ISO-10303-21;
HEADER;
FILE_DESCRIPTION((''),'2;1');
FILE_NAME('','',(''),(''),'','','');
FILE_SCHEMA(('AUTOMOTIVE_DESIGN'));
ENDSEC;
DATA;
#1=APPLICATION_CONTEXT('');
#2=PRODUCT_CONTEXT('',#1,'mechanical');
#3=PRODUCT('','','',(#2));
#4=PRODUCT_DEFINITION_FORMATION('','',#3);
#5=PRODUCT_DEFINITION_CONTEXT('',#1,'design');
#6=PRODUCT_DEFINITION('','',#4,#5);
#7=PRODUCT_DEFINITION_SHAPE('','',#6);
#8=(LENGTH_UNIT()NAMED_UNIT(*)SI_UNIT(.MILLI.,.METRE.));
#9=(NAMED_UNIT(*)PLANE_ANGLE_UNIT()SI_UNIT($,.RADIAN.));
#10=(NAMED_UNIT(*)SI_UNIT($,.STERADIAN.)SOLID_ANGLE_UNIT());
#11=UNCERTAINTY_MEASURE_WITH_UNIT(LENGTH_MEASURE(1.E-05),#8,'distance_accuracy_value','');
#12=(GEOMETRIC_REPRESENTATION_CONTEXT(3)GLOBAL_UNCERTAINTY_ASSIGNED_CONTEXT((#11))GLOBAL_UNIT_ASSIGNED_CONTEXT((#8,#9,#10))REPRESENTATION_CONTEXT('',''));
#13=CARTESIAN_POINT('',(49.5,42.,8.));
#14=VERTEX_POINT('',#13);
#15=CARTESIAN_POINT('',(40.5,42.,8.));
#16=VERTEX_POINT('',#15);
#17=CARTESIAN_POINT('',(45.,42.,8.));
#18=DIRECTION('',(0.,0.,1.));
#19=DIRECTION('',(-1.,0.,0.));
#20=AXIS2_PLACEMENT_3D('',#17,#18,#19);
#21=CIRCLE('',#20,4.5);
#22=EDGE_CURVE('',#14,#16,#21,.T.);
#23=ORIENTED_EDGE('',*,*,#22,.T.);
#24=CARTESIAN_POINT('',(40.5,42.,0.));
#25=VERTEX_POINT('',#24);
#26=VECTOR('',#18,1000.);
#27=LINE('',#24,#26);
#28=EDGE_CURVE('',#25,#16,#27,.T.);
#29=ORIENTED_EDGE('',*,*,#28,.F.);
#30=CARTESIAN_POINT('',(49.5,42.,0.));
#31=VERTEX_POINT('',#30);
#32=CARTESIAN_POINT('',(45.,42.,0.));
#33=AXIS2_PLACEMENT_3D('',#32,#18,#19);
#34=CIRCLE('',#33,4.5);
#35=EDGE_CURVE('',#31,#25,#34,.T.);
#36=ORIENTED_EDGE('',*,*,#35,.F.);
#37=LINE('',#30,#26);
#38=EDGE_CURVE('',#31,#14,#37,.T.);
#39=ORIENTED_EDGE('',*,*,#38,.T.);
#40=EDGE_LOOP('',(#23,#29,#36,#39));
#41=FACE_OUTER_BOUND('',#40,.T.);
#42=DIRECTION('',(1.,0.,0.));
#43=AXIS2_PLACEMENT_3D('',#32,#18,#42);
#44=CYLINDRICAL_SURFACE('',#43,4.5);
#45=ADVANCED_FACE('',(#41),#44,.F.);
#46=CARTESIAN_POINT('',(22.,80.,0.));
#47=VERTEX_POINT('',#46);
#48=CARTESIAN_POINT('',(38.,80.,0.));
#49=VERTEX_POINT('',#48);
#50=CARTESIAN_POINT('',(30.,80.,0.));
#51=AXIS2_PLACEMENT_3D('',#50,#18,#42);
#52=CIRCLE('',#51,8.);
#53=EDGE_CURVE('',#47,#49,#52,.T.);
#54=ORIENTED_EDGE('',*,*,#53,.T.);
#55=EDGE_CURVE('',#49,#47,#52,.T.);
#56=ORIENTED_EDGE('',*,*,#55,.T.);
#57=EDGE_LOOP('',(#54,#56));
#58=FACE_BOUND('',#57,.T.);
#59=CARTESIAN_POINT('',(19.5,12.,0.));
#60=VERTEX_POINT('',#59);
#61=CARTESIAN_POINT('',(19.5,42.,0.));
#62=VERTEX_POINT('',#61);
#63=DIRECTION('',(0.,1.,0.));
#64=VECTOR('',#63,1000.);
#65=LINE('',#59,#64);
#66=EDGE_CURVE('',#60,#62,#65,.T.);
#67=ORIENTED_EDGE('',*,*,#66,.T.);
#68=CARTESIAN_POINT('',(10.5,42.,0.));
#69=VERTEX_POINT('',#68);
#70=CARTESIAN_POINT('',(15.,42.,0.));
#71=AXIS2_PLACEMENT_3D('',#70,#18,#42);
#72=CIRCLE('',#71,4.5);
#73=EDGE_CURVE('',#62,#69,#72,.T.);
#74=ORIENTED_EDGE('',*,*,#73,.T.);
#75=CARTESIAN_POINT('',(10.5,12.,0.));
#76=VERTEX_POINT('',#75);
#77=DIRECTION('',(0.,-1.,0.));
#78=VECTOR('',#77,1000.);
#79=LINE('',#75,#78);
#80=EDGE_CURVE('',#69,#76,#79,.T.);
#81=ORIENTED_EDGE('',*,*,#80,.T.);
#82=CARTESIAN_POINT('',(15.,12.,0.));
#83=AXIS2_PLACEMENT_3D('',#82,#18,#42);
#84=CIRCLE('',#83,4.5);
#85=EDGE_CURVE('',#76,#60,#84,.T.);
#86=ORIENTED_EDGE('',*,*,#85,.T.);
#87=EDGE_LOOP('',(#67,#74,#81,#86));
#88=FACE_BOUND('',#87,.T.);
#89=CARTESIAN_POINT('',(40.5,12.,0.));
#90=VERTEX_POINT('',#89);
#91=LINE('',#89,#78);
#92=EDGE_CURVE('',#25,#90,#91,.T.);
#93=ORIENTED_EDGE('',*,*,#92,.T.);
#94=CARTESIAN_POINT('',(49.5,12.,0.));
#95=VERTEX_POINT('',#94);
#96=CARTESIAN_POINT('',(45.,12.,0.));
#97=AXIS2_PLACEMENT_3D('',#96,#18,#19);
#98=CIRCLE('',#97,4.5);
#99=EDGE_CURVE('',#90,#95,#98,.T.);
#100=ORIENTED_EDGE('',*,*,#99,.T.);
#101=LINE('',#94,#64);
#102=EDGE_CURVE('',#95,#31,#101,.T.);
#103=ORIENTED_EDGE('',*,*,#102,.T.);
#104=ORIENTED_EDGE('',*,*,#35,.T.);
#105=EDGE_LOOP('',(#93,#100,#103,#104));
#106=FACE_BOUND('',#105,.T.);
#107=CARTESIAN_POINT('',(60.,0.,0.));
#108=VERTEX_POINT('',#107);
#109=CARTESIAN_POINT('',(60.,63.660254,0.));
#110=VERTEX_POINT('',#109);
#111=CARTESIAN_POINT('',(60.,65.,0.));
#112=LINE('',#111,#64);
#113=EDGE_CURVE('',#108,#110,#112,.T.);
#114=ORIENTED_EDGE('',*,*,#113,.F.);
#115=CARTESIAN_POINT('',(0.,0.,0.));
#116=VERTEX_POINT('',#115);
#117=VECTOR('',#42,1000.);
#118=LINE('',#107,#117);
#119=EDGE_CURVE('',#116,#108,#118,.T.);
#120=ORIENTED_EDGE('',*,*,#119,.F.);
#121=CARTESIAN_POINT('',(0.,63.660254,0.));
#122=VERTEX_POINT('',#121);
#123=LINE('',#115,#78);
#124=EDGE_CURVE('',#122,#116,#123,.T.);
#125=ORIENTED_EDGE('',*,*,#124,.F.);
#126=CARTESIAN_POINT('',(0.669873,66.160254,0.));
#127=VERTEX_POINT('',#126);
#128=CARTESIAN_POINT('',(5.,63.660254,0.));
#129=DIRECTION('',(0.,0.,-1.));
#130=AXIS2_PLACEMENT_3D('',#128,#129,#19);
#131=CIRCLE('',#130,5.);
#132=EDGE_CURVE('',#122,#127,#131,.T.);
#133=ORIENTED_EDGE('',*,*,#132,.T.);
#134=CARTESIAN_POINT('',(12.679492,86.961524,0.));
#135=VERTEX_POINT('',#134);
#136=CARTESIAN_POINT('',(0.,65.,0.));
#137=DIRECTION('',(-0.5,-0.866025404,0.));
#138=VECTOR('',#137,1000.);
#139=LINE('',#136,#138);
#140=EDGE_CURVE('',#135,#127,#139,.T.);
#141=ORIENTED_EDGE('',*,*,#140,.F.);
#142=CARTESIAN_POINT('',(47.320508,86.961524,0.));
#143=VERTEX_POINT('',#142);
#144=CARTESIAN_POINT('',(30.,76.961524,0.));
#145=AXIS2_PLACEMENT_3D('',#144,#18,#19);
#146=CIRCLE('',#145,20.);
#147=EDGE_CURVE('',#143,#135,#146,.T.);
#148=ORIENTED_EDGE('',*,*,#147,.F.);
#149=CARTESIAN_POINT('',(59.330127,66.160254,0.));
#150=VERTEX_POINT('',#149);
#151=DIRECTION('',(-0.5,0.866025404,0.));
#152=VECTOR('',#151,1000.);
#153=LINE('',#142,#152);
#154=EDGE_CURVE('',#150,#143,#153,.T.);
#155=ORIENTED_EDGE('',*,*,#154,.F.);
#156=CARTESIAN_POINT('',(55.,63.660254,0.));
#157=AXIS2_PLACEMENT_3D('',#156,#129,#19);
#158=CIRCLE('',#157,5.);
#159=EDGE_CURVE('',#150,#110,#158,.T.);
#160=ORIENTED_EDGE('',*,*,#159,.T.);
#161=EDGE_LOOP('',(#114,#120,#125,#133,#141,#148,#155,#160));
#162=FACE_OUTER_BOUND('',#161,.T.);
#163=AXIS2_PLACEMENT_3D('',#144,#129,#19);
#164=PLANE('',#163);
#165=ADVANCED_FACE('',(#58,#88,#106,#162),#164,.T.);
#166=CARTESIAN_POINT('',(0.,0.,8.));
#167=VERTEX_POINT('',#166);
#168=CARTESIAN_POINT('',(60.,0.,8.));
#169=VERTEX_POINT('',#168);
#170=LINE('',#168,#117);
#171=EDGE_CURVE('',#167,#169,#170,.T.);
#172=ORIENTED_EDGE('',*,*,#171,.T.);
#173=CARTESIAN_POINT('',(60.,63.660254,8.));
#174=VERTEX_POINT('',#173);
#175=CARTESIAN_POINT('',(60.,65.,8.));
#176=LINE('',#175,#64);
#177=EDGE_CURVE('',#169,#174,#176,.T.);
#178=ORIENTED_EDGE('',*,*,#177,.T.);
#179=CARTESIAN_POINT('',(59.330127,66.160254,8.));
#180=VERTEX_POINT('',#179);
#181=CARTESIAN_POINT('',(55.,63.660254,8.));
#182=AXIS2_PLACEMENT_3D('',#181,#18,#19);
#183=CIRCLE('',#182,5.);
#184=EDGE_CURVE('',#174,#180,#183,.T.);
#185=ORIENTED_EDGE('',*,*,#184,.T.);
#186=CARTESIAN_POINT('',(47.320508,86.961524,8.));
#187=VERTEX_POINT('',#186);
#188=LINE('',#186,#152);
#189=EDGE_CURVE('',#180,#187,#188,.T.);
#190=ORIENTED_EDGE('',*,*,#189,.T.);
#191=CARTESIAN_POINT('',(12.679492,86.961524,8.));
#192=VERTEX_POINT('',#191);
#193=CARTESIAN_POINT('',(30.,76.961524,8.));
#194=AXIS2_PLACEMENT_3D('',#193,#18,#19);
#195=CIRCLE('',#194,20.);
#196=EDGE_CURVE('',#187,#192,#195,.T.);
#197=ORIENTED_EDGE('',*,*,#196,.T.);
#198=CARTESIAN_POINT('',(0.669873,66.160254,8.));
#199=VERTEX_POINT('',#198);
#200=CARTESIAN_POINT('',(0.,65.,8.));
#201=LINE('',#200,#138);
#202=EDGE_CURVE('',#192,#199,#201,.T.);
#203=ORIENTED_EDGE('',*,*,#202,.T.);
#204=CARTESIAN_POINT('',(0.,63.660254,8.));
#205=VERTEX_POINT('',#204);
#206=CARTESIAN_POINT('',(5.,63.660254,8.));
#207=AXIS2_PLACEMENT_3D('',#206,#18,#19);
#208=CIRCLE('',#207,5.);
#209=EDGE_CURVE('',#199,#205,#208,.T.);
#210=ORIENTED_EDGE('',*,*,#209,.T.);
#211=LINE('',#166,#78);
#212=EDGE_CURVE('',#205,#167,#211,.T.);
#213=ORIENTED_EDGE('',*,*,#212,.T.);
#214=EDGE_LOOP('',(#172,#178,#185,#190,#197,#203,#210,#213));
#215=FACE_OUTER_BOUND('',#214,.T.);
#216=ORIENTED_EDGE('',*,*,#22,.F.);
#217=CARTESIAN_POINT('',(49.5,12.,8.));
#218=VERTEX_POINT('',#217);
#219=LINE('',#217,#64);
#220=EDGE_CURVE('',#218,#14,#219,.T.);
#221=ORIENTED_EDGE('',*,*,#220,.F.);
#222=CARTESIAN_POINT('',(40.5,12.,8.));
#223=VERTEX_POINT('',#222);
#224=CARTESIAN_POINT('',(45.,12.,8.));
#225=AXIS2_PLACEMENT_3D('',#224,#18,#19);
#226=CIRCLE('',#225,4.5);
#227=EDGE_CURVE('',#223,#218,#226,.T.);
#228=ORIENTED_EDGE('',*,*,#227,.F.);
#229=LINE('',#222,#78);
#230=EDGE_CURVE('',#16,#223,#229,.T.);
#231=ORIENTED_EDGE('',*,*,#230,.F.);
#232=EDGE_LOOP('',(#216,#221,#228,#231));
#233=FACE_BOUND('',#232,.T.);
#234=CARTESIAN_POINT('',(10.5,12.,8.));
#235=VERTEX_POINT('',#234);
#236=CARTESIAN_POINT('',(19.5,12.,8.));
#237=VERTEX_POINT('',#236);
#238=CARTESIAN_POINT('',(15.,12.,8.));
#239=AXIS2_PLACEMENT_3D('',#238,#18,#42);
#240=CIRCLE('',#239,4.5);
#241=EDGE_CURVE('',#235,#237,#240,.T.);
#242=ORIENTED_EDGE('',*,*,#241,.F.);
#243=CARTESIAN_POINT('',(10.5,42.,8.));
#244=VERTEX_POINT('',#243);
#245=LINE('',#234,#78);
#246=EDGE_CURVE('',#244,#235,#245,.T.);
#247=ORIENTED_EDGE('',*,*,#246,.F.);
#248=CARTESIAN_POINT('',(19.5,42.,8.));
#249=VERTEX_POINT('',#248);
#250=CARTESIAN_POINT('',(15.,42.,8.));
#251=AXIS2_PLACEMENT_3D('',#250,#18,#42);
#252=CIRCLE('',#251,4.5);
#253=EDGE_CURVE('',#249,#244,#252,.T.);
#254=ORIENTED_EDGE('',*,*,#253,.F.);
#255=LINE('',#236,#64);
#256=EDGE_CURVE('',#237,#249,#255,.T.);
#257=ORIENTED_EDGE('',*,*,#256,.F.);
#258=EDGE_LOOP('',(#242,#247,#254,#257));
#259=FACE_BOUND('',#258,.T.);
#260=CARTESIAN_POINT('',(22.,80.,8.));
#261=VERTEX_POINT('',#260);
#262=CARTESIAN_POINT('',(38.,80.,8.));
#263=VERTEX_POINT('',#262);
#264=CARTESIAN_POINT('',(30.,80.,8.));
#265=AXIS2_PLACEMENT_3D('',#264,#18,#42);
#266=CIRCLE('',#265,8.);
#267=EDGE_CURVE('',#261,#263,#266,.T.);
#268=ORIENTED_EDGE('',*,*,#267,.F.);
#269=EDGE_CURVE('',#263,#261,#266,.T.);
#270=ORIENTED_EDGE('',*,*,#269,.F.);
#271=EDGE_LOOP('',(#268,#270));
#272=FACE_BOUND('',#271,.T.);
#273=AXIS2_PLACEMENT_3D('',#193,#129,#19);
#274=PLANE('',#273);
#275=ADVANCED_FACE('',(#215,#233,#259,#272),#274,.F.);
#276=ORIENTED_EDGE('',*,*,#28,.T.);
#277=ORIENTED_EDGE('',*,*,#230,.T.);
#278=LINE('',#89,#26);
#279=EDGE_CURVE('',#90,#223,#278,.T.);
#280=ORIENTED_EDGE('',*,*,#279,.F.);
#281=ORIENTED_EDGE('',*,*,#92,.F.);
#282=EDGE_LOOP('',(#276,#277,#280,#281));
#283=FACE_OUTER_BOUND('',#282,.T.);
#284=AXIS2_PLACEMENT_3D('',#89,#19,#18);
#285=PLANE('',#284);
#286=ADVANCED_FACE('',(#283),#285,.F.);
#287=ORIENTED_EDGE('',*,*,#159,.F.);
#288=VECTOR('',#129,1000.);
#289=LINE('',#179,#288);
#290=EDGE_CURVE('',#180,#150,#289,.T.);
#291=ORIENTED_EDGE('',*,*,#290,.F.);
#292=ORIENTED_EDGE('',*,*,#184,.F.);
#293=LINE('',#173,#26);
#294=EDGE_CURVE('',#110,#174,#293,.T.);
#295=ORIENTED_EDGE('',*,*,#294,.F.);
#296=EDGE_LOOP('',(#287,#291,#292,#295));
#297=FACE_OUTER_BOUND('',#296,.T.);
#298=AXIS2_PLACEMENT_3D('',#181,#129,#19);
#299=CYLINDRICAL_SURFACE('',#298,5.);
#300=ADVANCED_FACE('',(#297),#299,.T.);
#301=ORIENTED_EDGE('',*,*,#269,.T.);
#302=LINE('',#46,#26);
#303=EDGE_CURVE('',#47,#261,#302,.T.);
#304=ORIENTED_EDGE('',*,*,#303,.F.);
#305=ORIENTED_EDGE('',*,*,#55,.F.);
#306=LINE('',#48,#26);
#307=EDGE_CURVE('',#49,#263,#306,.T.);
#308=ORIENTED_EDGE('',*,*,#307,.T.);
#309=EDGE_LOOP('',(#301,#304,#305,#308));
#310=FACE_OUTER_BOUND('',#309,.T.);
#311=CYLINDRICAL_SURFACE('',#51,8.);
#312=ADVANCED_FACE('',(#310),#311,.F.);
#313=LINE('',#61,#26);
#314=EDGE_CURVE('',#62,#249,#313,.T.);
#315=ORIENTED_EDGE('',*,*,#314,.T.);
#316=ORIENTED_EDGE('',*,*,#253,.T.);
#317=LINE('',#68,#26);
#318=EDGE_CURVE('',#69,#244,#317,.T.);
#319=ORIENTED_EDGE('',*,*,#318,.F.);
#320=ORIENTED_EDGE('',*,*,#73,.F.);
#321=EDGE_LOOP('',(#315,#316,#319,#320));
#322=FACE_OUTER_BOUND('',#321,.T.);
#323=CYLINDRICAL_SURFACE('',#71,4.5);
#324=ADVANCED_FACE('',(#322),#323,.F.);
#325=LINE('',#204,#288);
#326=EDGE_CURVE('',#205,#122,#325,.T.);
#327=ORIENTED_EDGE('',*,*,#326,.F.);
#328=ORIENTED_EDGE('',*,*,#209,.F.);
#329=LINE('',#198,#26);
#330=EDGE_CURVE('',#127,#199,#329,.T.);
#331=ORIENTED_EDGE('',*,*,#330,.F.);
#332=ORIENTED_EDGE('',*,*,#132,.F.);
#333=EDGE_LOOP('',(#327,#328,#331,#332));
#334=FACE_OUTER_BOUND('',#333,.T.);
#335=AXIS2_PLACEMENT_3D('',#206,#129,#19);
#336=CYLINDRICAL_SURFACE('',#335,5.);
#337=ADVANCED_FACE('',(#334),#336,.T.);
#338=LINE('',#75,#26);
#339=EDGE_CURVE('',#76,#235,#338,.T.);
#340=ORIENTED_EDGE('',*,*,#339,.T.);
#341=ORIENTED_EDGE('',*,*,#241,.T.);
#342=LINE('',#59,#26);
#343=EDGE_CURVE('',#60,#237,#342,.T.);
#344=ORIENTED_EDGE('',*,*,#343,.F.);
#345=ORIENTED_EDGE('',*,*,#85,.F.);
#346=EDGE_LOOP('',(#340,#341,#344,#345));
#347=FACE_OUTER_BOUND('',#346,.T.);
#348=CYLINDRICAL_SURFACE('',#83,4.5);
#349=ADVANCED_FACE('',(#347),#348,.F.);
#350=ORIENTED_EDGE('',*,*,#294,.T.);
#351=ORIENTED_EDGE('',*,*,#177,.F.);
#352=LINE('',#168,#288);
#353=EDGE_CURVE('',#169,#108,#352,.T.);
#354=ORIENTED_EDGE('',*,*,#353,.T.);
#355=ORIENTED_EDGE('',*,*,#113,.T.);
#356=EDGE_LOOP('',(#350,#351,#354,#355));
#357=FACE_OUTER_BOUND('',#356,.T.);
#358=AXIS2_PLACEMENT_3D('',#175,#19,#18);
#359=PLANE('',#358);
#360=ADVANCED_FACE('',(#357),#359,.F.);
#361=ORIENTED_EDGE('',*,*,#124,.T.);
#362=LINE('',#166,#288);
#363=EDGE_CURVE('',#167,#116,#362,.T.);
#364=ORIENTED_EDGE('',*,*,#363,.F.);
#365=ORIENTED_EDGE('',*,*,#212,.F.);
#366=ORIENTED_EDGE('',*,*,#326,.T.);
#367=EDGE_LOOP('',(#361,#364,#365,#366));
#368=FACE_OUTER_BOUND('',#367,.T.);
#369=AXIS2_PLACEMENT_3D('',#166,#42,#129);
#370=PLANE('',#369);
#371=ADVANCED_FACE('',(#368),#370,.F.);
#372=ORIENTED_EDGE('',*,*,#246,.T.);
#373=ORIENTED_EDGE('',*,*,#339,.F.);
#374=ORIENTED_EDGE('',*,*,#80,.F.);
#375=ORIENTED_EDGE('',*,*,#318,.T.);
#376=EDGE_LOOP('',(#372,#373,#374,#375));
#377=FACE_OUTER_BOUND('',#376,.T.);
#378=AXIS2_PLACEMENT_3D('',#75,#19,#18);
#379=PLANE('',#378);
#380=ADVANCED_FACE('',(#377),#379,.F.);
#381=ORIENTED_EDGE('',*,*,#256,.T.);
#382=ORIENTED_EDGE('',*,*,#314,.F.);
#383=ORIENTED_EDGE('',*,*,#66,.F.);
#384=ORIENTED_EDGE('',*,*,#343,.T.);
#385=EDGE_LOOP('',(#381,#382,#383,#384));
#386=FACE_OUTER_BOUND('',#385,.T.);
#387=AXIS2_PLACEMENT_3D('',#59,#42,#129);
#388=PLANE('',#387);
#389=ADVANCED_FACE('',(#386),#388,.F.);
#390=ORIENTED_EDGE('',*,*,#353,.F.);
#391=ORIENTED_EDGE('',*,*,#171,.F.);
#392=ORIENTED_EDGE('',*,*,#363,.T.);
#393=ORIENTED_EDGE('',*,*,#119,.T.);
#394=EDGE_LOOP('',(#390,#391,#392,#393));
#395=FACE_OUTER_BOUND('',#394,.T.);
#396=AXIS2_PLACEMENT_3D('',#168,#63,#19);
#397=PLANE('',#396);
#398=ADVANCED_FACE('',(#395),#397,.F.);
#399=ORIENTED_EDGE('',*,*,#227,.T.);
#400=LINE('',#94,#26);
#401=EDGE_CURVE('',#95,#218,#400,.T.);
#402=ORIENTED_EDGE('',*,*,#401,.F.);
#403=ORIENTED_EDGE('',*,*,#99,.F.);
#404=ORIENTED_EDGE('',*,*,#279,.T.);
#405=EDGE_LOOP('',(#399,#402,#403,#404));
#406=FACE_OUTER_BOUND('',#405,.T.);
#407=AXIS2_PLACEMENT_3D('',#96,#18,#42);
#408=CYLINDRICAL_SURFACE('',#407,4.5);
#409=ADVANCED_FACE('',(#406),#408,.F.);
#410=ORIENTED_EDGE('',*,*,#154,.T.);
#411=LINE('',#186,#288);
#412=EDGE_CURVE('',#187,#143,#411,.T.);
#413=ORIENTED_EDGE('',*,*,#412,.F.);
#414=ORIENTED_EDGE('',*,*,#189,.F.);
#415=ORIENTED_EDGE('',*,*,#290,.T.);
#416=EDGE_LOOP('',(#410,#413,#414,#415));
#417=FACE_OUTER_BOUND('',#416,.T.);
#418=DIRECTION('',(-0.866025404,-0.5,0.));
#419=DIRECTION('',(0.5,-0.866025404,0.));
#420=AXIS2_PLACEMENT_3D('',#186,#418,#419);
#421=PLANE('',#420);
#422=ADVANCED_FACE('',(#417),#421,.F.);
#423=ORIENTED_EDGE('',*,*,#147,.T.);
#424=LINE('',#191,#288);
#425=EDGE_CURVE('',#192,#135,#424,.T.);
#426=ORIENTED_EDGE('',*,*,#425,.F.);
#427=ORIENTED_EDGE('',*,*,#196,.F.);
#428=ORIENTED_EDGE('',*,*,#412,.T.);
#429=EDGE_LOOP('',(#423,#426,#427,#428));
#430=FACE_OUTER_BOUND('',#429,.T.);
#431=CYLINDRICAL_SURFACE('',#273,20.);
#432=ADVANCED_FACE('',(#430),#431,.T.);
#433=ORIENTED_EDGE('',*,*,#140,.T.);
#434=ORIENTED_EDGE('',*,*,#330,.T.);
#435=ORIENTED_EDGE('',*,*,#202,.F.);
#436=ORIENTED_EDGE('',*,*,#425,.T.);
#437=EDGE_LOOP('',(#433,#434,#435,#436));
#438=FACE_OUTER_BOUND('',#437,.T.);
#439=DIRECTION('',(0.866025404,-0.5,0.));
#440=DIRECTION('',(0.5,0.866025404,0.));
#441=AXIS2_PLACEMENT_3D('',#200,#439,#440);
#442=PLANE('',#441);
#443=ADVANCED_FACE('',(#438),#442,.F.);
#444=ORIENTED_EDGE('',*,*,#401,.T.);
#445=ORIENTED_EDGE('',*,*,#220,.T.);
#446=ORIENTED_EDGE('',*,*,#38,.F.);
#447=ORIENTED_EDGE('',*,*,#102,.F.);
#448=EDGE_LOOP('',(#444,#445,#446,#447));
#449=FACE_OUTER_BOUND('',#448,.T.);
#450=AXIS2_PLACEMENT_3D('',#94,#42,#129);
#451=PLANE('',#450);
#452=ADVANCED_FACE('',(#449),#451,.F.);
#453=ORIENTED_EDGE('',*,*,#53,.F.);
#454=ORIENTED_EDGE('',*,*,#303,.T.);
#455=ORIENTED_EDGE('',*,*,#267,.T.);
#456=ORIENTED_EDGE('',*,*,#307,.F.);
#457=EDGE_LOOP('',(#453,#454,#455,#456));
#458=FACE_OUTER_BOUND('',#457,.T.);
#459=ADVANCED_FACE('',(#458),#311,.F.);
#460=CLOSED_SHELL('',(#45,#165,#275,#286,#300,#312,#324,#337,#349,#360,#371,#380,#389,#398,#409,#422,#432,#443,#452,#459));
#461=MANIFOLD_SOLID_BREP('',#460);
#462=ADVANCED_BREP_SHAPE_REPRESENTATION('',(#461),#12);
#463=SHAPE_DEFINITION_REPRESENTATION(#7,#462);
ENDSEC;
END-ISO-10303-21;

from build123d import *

# Parameters (mm, degrees)
BOSS_EXTRUDE1_DEPTH = 8
SKETCH3_R           = 8
CUT_EXTRUDE1_DEPTH  = 8
CUT_EXTRUDE2_DEPTH  = 115.30458075
FILLET1_R           = 5


with BuildPart() as part:
    # Sketch2 → Boss-Extrude1 (new body)
    with BuildSketch(Plane.XY):
        with BuildLine():
            Line((0, 0), (0, 65))
            Line((0, 65), (12.679491924, 86.961524227))
            ThreePointArc((12.679491924, 86.961524227), (30, 96.961524227), (47.320508076, 86.961524227))
            Line((47.320508076, 86.961524227), (60, 65))
            Line((60, 65), (60, 0))
            Line((60, 0), (0, 0))
        make_face()
    extrude(amount=BOSS_EXTRUDE1_DEPTH)

    # Sketch3 → Cut-Extrude1 (cut)
    with BuildSketch(Plane.XY.offset(8)):
        with Locations((30, 80)):
            Circle(SKETCH3_R)
    extrude(amount=-CUT_EXTRUDE1_DEPTH, mode=Mode.SUBTRACT)

    # Sketch4 → Cut-Extrude2 (cut, through all)
    with BuildSketch(Plane.XY.offset(8)):
        with BuildLine():
            Line((10.5, 12), (10.5, 42))
            ThreePointArc((10.5, 42), (15, 46.5), (19.5, 42))
            Line((19.5, 42), (19.5, 12))
            ThreePointArc((19.5, 12), (15, 7.5), (10.5, 12))
        make_face()
        with BuildLine():
            Line((49.5, 12), (49.5, 42))
            ThreePointArc((49.5, 42), (45, 46.5), (40.5, 42))
            Line((40.5, 42), (40.5, 12))
            ThreePointArc((40.5, 12), (45, 7.5), (49.5, 12))
        make_face()
    extrude(amount=-CUT_EXTRUDE2_DEPTH, mode=Mode.SUBTRACT)

    # Fillet1
    fillet1_edges = [part.edges().sort_by_distance(p)[0] for p in [
        (0, 65, 4),
        (60, 65, 4),
    ]]
    fillet(fillet1_edges, radius=FILLET1_R)


solid = part.part
